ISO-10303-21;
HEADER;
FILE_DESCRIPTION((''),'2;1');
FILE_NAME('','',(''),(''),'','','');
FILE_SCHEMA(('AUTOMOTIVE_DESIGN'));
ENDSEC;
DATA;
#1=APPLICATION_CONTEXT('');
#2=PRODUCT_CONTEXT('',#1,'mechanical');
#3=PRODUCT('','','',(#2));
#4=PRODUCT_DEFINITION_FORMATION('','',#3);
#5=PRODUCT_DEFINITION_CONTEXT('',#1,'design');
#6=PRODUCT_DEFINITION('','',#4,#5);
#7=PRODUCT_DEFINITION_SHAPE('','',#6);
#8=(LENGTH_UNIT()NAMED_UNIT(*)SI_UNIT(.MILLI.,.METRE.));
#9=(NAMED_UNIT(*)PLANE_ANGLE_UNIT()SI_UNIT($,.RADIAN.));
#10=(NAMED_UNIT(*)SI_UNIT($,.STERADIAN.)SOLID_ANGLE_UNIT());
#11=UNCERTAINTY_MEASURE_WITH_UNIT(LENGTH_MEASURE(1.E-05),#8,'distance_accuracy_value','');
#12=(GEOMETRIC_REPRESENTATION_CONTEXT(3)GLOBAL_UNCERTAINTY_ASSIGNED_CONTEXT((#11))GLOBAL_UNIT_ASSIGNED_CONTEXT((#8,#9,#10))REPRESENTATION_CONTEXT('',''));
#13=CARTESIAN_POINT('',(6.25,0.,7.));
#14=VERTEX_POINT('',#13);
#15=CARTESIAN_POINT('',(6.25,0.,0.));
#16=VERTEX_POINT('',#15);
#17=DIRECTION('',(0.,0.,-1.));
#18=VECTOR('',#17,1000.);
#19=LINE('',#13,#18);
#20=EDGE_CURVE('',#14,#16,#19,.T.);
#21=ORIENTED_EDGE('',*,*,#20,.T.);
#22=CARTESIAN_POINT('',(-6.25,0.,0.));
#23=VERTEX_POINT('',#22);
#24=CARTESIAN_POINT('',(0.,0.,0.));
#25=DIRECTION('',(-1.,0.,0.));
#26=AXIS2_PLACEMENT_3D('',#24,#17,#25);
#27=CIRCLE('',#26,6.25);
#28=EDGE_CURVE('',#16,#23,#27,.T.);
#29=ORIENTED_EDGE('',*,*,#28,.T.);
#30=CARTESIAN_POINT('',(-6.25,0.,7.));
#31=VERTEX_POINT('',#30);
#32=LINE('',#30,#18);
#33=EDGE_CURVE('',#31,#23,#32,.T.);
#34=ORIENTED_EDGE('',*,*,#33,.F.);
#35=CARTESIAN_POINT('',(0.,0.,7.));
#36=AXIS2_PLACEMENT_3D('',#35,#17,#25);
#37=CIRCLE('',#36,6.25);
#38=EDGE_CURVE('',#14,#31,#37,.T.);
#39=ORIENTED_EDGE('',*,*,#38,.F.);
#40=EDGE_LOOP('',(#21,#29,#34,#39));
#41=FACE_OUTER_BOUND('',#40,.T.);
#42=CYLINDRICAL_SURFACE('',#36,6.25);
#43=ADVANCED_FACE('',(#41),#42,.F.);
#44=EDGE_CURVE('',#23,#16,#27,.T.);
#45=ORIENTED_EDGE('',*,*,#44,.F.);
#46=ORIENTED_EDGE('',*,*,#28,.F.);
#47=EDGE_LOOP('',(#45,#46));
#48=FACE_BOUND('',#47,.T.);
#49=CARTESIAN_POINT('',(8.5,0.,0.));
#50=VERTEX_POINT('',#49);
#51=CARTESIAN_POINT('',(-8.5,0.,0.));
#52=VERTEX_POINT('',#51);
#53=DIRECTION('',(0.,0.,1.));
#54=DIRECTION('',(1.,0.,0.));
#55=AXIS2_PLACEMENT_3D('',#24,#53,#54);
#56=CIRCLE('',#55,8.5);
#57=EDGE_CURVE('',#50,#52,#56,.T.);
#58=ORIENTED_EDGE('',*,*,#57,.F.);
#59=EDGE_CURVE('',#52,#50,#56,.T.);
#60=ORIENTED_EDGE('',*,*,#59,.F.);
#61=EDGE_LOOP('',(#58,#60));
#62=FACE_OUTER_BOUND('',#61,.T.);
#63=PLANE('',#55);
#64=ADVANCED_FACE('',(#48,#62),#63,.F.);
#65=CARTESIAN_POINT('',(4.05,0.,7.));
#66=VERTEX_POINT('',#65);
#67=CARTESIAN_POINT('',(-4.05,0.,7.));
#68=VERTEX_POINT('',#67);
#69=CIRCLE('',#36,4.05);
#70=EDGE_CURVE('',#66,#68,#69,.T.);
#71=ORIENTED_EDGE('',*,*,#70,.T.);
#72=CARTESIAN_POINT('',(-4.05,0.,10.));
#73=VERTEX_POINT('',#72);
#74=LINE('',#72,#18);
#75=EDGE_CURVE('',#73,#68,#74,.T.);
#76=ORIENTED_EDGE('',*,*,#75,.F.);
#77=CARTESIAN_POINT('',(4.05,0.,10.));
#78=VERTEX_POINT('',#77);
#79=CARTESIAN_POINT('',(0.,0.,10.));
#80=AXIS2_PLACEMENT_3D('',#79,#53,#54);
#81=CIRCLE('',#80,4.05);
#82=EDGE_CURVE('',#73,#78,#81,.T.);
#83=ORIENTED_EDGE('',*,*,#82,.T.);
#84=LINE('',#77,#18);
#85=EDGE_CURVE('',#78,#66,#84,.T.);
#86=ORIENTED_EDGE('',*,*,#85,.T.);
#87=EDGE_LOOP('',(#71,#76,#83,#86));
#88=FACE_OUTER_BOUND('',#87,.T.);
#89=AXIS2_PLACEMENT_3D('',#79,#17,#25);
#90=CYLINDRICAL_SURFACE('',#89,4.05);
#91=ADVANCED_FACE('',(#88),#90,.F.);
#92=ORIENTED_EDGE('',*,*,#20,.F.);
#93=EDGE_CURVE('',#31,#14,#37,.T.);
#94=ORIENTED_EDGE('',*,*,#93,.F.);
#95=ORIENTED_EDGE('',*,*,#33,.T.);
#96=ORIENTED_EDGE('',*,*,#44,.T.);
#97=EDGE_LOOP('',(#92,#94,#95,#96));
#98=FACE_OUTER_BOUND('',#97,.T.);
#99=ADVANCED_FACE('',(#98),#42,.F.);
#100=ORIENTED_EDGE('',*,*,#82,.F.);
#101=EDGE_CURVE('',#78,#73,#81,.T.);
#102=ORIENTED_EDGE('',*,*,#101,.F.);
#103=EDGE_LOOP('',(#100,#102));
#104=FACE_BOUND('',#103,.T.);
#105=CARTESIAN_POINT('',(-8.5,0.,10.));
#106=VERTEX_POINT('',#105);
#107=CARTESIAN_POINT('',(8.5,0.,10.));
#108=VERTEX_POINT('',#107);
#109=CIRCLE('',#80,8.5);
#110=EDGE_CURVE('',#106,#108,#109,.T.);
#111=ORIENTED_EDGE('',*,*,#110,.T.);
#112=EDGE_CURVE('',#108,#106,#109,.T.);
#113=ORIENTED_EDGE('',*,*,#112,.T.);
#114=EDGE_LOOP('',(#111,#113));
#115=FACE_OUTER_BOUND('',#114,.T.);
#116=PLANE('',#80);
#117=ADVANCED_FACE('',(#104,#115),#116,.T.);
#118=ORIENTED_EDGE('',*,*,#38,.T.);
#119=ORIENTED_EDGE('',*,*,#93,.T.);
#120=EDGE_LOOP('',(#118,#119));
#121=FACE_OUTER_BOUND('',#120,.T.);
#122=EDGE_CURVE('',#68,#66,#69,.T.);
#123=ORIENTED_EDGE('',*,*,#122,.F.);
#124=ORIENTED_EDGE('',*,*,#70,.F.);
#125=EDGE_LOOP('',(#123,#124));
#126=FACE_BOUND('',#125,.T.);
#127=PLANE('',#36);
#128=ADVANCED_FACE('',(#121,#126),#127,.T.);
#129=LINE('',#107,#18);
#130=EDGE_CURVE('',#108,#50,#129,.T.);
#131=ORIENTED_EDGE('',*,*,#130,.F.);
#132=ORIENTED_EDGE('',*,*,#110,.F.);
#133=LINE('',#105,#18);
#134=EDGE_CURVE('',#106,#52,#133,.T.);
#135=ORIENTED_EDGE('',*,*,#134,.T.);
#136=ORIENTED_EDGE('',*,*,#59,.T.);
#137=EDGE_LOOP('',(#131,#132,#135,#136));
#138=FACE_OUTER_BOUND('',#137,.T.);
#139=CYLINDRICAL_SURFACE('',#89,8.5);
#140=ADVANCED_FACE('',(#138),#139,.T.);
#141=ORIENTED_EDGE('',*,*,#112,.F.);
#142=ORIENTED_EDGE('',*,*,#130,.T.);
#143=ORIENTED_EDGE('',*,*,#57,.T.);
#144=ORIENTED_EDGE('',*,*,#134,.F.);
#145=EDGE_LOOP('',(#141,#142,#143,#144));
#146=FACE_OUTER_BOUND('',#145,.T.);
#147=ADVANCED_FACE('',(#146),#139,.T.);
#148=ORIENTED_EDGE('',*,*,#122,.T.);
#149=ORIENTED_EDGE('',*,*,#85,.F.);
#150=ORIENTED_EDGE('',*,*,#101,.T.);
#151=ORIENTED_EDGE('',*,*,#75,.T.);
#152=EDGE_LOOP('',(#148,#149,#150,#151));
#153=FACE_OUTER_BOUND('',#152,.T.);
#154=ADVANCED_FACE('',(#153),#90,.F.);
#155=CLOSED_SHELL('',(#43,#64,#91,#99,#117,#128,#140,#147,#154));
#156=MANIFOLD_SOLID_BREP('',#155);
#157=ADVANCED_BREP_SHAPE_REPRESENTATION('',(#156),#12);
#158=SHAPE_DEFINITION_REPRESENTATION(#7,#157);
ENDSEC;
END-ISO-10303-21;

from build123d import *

# Parameters (mm, degrees)
SKETCH_1_R          = 8.5
SKETCH_1_R_2        = 4.05
EXTRUDE_1_DEPTH     = 10
SKETCH_2_R          = 6.25
CUT_EXTRUDE_1_DEPTH = 7


with BuildPart() as part:
    # 草图1 → 凸台-拉伸1 (new body)
    with BuildSketch(Plane.XY):
        Circle(SKETCH_1_R)
        Circle(SKETCH_1_R_2, mode=Mode.SUBTRACT)
    extrude(amount=EXTRUDE_1_DEPTH)

    # 草图2 → 切除-拉伸1 (cut)
    with BuildSketch(Plane(origin=(0, 0, 0), x_dir=(-1, 0, 0), z_dir=(0, 0, -1))):
        Circle(SKETCH_2_R)
    extrude(amount=-CUT_EXTRUDE_1_DEPTH, mode=Mode.SUBTRACT)


solid = part.part
